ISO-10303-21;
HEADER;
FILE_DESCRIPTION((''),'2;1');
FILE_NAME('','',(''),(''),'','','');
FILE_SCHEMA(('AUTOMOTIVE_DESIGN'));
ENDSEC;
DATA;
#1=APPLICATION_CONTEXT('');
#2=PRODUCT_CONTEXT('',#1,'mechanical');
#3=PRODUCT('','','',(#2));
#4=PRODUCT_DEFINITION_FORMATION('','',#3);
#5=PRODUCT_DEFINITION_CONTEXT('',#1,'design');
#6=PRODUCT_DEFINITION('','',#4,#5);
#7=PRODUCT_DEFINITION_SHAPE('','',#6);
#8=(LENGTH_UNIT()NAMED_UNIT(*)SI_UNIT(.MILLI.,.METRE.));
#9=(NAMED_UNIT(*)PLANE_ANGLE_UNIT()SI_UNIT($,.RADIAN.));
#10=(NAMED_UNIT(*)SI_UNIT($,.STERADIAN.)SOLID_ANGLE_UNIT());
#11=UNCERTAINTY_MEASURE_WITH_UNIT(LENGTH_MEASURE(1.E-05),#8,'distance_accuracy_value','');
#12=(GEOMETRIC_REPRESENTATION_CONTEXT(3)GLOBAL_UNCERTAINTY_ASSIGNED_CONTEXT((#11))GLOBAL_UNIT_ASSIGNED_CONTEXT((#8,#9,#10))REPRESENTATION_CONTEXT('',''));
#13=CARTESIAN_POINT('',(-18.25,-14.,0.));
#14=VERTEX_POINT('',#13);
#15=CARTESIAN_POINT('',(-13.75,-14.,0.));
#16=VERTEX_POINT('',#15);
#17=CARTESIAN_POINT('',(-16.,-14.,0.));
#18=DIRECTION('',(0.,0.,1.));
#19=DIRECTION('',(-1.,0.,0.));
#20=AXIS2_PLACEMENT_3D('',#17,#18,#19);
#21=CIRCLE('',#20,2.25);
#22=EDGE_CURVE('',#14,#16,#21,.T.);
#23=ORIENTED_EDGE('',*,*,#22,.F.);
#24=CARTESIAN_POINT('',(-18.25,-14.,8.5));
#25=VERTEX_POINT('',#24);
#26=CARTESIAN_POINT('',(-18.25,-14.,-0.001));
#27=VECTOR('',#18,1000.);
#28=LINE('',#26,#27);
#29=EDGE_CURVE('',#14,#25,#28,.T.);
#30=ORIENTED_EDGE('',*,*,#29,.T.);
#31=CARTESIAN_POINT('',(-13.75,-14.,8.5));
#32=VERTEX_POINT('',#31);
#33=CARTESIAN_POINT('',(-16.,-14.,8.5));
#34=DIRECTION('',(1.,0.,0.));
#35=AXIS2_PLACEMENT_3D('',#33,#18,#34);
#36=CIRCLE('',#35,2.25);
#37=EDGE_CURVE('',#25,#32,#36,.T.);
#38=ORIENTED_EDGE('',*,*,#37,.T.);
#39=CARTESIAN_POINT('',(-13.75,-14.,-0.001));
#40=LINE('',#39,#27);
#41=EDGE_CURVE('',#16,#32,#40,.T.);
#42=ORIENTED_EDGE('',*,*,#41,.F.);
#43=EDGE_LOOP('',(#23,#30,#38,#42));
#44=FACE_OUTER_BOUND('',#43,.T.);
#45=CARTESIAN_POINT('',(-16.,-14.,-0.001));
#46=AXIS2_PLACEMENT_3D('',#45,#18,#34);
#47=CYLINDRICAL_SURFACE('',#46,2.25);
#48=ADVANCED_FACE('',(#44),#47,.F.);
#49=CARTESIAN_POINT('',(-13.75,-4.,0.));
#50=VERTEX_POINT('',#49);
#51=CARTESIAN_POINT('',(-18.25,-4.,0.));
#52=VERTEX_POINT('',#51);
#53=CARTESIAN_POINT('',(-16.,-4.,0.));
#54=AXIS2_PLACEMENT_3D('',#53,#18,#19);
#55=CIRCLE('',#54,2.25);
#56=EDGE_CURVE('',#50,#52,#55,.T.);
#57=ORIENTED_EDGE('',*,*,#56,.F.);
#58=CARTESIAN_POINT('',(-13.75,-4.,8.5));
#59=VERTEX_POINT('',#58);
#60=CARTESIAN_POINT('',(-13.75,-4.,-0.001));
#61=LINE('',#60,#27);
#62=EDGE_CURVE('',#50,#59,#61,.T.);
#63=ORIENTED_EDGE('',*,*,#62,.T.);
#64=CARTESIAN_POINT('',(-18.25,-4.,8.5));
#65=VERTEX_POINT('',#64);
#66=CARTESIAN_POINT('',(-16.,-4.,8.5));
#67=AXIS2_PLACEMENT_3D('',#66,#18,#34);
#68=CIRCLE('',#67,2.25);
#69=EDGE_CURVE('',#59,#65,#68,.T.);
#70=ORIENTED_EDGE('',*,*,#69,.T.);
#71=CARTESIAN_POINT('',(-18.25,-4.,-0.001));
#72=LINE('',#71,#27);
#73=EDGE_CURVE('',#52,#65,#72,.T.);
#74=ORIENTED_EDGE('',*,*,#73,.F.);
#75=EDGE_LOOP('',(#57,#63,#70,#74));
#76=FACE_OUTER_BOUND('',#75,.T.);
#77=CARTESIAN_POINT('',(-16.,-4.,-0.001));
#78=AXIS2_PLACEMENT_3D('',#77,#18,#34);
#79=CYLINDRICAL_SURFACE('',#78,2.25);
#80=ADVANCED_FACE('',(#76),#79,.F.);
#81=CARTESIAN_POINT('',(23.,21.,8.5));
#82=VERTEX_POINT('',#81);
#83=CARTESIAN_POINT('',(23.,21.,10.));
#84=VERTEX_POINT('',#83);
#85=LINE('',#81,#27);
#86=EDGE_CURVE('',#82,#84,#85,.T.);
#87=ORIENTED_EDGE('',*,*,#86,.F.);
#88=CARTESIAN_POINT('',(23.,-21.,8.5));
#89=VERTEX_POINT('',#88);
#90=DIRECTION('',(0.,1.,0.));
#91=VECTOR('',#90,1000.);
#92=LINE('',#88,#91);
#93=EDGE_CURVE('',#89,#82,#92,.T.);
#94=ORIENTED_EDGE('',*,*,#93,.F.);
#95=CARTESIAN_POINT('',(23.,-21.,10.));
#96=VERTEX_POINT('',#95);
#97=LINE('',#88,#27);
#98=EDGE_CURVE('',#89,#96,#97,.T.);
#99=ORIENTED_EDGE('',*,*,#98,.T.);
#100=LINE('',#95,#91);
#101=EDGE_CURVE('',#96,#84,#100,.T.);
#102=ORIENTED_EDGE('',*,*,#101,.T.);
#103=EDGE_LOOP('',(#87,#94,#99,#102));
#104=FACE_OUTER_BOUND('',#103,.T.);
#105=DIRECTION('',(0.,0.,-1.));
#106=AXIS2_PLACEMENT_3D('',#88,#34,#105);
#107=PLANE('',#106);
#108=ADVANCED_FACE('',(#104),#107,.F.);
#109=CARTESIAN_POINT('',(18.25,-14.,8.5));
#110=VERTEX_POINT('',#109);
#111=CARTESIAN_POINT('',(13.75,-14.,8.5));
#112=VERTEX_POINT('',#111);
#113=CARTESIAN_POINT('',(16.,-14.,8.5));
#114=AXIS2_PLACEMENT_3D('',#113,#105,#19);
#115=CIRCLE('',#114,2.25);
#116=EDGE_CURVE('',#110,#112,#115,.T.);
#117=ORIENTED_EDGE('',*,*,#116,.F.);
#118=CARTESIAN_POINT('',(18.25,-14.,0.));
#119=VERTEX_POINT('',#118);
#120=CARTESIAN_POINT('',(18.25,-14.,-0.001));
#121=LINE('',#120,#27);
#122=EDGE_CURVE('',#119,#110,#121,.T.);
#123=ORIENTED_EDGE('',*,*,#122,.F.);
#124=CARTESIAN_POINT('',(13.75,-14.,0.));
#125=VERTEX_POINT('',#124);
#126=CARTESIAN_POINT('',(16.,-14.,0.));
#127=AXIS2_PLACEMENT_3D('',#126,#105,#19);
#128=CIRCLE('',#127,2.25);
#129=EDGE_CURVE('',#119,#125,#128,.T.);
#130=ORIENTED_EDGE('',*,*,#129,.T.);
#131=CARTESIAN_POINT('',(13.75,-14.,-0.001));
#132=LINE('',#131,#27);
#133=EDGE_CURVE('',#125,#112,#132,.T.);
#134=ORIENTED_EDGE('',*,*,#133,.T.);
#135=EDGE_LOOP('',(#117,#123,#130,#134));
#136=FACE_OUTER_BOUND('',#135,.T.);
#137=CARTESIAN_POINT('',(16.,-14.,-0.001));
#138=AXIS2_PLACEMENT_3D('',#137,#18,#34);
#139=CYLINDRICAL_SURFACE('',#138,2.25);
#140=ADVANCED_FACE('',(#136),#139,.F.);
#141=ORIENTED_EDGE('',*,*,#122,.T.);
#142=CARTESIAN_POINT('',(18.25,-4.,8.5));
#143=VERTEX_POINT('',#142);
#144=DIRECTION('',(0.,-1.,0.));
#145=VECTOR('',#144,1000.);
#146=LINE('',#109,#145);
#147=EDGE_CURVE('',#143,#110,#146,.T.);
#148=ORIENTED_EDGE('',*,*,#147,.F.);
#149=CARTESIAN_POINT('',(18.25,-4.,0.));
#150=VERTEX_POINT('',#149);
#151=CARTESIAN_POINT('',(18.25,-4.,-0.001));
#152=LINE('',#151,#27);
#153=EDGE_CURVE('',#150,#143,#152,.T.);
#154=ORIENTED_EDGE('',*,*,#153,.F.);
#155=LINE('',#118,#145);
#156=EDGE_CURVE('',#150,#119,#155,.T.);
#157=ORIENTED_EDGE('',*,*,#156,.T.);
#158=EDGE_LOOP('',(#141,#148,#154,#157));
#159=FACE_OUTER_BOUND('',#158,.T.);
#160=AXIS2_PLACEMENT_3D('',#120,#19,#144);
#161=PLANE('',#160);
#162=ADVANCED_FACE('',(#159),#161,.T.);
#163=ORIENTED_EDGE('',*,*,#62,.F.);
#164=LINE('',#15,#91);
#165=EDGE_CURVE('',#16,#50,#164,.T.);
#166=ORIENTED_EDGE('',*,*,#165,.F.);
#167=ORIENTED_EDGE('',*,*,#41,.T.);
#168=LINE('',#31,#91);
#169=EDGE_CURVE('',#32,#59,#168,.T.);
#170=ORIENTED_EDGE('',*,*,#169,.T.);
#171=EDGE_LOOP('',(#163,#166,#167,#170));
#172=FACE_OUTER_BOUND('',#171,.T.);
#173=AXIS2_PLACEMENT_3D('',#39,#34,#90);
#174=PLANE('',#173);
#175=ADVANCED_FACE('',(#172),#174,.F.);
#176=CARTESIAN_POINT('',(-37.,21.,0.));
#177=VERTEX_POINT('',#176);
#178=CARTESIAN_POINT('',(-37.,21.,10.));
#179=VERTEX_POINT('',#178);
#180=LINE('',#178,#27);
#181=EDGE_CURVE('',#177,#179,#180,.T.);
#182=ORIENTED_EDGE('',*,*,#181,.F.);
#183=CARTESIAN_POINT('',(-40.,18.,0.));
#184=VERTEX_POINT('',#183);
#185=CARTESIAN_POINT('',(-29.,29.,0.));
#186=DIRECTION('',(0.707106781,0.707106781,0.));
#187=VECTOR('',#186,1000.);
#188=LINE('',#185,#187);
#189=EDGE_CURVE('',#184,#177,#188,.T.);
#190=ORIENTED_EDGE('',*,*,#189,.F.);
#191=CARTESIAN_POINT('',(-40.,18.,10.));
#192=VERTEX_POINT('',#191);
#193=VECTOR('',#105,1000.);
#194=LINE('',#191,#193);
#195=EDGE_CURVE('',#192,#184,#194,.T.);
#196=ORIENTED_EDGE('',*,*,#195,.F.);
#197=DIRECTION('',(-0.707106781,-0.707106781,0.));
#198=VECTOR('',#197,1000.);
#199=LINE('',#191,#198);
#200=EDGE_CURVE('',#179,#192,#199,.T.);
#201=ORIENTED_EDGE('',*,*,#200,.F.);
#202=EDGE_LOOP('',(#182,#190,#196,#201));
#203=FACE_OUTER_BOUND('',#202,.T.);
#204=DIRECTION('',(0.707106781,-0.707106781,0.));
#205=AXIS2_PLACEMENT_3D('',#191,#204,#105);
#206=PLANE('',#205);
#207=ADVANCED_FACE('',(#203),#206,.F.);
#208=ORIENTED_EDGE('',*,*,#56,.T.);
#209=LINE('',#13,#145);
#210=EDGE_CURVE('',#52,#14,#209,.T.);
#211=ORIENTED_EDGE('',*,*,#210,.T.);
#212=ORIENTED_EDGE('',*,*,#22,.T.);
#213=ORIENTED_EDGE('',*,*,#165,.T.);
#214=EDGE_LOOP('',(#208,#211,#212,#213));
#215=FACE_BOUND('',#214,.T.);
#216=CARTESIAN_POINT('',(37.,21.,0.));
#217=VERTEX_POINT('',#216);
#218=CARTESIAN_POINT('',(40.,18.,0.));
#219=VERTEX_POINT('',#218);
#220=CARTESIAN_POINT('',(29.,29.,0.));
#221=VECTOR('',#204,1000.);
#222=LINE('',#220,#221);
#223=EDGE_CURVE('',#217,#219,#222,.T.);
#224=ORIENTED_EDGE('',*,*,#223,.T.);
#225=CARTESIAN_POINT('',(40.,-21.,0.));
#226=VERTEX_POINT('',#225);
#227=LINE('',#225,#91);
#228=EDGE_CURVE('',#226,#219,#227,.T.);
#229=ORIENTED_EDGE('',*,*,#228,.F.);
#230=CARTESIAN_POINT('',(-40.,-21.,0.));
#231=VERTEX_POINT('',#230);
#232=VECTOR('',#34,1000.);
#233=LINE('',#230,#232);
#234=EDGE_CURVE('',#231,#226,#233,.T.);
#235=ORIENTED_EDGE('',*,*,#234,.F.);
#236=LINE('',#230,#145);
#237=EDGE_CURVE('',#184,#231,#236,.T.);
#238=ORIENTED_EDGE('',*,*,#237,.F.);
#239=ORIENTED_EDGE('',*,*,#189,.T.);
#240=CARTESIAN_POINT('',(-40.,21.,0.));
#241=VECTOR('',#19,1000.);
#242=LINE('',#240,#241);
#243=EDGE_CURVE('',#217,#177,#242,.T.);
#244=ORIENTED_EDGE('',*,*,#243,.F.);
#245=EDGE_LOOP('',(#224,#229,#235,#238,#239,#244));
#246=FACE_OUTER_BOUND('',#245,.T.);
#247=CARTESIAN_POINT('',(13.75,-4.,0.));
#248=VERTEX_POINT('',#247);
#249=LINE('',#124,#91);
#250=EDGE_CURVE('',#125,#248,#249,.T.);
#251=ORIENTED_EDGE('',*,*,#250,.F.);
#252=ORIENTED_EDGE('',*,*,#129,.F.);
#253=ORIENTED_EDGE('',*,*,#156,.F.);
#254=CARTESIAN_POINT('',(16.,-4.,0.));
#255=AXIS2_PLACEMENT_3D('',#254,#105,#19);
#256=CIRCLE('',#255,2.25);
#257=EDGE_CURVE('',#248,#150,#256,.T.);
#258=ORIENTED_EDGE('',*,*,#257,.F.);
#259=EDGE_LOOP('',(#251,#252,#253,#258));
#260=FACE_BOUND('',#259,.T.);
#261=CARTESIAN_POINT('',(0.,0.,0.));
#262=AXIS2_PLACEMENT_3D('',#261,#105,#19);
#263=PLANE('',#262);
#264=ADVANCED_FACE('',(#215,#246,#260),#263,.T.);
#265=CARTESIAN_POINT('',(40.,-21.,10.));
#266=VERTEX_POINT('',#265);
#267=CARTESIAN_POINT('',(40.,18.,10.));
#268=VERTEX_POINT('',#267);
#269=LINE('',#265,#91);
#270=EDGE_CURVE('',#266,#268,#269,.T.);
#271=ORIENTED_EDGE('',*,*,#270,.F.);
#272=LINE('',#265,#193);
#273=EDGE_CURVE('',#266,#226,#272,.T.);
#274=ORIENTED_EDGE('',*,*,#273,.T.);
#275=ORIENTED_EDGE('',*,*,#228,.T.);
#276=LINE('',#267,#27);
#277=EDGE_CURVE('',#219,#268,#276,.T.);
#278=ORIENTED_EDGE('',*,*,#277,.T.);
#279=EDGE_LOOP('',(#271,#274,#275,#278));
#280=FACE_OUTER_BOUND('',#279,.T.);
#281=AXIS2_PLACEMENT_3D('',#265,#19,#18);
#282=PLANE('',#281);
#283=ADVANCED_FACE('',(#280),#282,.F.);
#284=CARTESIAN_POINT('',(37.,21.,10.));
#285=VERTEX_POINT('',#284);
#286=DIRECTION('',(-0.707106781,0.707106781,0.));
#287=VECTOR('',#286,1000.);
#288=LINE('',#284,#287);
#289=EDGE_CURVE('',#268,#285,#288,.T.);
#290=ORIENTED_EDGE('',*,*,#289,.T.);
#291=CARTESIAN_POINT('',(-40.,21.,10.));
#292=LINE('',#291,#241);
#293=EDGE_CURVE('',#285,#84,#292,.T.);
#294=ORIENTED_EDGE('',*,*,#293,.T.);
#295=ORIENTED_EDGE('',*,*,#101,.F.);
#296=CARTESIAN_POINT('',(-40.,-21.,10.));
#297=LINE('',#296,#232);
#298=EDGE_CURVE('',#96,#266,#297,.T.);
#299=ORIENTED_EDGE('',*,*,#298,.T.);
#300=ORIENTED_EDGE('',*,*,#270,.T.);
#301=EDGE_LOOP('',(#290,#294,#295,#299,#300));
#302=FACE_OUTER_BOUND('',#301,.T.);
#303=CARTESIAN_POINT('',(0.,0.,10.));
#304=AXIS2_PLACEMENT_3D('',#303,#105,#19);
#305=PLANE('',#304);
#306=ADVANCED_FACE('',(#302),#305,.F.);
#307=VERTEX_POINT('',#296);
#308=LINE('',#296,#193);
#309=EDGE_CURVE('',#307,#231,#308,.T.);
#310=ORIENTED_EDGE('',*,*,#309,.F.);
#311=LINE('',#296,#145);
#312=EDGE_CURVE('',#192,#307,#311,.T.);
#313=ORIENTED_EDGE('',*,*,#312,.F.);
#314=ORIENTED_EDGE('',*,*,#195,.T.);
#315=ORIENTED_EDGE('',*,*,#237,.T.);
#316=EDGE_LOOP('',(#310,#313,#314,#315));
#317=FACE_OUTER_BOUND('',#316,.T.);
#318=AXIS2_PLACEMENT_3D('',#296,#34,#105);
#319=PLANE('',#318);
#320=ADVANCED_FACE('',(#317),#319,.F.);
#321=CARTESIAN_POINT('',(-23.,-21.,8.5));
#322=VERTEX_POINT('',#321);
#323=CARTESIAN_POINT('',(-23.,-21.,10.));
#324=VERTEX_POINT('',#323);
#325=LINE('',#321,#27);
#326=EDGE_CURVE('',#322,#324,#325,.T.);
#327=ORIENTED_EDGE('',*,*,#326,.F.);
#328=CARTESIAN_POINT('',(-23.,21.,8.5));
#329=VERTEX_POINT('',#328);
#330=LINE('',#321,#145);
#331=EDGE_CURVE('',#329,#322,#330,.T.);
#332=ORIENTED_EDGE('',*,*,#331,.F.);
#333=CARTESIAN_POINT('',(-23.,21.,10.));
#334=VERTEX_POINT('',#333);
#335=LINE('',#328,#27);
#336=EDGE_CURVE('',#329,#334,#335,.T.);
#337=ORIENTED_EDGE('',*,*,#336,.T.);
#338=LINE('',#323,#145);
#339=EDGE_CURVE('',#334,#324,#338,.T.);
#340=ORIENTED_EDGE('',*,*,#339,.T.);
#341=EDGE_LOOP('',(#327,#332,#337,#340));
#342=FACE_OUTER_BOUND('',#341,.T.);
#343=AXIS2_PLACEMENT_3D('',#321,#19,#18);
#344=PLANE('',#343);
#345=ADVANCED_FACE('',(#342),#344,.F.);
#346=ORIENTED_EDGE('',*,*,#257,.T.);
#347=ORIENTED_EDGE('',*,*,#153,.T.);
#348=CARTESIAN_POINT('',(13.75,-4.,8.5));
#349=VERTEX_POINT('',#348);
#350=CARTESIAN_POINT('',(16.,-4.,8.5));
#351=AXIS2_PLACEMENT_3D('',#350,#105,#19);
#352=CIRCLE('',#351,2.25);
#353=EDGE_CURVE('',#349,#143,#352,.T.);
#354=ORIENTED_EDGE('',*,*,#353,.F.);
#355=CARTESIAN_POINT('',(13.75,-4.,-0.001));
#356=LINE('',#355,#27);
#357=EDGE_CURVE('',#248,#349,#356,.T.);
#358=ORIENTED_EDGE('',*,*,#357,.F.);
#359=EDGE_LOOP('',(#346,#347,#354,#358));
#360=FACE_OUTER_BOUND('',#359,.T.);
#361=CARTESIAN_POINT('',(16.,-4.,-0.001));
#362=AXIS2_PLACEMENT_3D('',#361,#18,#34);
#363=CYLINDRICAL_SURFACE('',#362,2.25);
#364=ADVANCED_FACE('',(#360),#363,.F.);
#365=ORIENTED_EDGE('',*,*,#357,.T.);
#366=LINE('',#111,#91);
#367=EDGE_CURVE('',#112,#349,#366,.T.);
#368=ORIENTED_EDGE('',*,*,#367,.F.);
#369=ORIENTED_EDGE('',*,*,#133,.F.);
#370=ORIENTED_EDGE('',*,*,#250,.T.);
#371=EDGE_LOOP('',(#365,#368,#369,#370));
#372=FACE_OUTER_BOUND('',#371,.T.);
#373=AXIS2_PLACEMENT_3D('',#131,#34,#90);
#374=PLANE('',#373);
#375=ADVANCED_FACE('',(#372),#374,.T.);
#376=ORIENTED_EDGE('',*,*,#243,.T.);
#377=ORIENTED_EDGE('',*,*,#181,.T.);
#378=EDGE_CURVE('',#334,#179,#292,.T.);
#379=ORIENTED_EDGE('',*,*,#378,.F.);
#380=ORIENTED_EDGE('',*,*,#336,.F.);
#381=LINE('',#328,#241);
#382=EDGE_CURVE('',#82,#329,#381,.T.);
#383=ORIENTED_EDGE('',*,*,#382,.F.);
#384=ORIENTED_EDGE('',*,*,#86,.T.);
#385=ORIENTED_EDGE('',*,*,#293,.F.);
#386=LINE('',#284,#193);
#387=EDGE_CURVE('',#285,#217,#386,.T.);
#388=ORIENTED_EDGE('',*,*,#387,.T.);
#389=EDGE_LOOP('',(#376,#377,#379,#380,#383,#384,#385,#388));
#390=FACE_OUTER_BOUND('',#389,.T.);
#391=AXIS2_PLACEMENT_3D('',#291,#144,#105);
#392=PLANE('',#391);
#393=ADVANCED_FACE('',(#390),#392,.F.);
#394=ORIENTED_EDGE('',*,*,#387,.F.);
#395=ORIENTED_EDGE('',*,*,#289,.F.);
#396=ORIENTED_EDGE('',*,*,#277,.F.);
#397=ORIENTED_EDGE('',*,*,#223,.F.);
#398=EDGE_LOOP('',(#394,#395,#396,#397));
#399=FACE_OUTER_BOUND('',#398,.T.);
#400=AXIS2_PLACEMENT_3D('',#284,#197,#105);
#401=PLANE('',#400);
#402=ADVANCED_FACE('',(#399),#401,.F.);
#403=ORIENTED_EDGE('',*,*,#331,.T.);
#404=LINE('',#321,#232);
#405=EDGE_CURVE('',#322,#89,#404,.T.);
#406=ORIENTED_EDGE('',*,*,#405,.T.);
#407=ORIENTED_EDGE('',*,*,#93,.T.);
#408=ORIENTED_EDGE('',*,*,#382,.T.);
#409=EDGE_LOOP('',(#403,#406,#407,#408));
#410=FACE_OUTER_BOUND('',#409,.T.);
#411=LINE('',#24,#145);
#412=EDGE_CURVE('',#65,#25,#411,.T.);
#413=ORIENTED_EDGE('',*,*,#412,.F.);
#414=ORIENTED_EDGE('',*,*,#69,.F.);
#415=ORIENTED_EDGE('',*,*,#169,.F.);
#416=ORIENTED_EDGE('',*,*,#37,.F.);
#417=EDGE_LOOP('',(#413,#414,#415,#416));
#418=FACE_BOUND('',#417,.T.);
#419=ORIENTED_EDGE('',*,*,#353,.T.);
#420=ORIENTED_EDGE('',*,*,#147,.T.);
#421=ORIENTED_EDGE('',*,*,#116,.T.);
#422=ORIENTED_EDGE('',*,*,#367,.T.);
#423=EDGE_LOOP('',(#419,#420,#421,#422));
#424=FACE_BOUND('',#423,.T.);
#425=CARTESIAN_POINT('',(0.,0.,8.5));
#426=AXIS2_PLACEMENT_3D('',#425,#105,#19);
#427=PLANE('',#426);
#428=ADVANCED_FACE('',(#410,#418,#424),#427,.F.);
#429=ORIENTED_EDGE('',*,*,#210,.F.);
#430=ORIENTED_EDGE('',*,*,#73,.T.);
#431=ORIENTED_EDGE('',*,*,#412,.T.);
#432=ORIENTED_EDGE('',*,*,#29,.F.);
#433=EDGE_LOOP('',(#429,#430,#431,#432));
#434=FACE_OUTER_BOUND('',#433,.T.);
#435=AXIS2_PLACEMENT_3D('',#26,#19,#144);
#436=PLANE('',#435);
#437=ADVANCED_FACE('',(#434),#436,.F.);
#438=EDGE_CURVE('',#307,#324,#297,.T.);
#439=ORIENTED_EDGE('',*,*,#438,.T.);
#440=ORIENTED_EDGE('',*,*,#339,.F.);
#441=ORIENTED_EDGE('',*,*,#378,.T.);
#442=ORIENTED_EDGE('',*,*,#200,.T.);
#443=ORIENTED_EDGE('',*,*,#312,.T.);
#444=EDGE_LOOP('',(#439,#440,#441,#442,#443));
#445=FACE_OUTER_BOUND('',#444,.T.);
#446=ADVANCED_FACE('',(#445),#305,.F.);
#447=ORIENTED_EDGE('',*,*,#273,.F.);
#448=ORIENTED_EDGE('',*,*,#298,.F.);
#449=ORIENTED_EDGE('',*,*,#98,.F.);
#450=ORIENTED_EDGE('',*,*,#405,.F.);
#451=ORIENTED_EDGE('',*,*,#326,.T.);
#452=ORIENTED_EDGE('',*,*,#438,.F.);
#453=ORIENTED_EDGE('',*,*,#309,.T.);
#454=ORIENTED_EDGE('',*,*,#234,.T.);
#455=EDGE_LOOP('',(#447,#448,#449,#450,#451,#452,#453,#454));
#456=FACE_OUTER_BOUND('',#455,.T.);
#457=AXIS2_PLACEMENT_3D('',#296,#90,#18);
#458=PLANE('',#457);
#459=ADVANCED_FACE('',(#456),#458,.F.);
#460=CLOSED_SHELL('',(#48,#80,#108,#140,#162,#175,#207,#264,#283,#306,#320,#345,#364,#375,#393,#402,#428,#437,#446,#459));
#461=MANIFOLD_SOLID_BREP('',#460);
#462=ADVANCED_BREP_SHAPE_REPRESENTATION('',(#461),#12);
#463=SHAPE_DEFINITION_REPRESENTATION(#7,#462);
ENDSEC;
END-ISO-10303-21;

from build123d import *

# Parameters (mm, degrees)
SKETCH_1_W          = 80
SKETCH_1_H          = 42
EXTRUDE_1_DEPTH     = 10
SKETCH_2_W          = 46
SKETCH_2_H          = 42
CUT_EXTRUDE_1_DEPTH = 1.5
CHAMFER_1_SIZE      = 3
CUT_EXTRUDE_2_REACH = 47.97


with BuildPart() as part:
    # 草图1 → 凸台-拉伸1 (new body)
    with BuildSketch(Plane.XY):
        Rectangle(SKETCH_1_W, SKETCH_1_H)
    extrude(amount=EXTRUDE_1_DEPTH)

    # 草图2 → 切除-拉伸1 (cut)
    with BuildSketch(Plane.XY.offset(10)):
        Rectangle(SKETCH_2_W, SKETCH_2_H)
    extrude(amount=-CUT_EXTRUDE_1_DEPTH, mode=Mode.SUBTRACT)

    # 倒角1
    chamfer_1_edges = [part.edges().sort_by_distance(p)[0] for p in [
        (-40, 21, 5),
        (40, 21, 5),
    ]]
    chamfer(chamfer_1_edges, length=CHAMFER_1_SIZE)

    # 草图3 → 切除-拉伸2 (cut, up to next)
    with BuildSketch(Plane.XY.offset(8.5), mode=Mode.PRIVATE) as cut_extrude_2_sk1:
        with BuildLine():
            Line((-18.25, -14), (-18.25, -4))
            ThreePointArc((-18.25, -4), (-16, -1.75), (-13.75, -4))
            Line((-13.75, -4), (-13.75, -14))
            ThreePointArc((-13.75, -14), (-16, -16.25), (-18.25, -14))
        make_face()
    cut_extrude_2_tool1 = extrude(cut_extrude_2_sk1.sketch, amount=-CUT_EXTRUDE_2_REACH, mode=Mode.PRIVATE) & part.part
    cut_extrude_2 = cut_extrude_2_tool1.solids().sort_by_distance((-16, -9, 8.5))[0]
    add(cut_extrude_2, mode=Mode.SUBTRACT)

    # 镜向1: 切除-拉伸2 across plane
    add(cut_extrude_2.mirror(Plane(origin=(0, 0, 0), x_dir=(0, 0, 1), z_dir=(1, 0, 0))), mode=Mode.SUBTRACT)


solid = part.part
